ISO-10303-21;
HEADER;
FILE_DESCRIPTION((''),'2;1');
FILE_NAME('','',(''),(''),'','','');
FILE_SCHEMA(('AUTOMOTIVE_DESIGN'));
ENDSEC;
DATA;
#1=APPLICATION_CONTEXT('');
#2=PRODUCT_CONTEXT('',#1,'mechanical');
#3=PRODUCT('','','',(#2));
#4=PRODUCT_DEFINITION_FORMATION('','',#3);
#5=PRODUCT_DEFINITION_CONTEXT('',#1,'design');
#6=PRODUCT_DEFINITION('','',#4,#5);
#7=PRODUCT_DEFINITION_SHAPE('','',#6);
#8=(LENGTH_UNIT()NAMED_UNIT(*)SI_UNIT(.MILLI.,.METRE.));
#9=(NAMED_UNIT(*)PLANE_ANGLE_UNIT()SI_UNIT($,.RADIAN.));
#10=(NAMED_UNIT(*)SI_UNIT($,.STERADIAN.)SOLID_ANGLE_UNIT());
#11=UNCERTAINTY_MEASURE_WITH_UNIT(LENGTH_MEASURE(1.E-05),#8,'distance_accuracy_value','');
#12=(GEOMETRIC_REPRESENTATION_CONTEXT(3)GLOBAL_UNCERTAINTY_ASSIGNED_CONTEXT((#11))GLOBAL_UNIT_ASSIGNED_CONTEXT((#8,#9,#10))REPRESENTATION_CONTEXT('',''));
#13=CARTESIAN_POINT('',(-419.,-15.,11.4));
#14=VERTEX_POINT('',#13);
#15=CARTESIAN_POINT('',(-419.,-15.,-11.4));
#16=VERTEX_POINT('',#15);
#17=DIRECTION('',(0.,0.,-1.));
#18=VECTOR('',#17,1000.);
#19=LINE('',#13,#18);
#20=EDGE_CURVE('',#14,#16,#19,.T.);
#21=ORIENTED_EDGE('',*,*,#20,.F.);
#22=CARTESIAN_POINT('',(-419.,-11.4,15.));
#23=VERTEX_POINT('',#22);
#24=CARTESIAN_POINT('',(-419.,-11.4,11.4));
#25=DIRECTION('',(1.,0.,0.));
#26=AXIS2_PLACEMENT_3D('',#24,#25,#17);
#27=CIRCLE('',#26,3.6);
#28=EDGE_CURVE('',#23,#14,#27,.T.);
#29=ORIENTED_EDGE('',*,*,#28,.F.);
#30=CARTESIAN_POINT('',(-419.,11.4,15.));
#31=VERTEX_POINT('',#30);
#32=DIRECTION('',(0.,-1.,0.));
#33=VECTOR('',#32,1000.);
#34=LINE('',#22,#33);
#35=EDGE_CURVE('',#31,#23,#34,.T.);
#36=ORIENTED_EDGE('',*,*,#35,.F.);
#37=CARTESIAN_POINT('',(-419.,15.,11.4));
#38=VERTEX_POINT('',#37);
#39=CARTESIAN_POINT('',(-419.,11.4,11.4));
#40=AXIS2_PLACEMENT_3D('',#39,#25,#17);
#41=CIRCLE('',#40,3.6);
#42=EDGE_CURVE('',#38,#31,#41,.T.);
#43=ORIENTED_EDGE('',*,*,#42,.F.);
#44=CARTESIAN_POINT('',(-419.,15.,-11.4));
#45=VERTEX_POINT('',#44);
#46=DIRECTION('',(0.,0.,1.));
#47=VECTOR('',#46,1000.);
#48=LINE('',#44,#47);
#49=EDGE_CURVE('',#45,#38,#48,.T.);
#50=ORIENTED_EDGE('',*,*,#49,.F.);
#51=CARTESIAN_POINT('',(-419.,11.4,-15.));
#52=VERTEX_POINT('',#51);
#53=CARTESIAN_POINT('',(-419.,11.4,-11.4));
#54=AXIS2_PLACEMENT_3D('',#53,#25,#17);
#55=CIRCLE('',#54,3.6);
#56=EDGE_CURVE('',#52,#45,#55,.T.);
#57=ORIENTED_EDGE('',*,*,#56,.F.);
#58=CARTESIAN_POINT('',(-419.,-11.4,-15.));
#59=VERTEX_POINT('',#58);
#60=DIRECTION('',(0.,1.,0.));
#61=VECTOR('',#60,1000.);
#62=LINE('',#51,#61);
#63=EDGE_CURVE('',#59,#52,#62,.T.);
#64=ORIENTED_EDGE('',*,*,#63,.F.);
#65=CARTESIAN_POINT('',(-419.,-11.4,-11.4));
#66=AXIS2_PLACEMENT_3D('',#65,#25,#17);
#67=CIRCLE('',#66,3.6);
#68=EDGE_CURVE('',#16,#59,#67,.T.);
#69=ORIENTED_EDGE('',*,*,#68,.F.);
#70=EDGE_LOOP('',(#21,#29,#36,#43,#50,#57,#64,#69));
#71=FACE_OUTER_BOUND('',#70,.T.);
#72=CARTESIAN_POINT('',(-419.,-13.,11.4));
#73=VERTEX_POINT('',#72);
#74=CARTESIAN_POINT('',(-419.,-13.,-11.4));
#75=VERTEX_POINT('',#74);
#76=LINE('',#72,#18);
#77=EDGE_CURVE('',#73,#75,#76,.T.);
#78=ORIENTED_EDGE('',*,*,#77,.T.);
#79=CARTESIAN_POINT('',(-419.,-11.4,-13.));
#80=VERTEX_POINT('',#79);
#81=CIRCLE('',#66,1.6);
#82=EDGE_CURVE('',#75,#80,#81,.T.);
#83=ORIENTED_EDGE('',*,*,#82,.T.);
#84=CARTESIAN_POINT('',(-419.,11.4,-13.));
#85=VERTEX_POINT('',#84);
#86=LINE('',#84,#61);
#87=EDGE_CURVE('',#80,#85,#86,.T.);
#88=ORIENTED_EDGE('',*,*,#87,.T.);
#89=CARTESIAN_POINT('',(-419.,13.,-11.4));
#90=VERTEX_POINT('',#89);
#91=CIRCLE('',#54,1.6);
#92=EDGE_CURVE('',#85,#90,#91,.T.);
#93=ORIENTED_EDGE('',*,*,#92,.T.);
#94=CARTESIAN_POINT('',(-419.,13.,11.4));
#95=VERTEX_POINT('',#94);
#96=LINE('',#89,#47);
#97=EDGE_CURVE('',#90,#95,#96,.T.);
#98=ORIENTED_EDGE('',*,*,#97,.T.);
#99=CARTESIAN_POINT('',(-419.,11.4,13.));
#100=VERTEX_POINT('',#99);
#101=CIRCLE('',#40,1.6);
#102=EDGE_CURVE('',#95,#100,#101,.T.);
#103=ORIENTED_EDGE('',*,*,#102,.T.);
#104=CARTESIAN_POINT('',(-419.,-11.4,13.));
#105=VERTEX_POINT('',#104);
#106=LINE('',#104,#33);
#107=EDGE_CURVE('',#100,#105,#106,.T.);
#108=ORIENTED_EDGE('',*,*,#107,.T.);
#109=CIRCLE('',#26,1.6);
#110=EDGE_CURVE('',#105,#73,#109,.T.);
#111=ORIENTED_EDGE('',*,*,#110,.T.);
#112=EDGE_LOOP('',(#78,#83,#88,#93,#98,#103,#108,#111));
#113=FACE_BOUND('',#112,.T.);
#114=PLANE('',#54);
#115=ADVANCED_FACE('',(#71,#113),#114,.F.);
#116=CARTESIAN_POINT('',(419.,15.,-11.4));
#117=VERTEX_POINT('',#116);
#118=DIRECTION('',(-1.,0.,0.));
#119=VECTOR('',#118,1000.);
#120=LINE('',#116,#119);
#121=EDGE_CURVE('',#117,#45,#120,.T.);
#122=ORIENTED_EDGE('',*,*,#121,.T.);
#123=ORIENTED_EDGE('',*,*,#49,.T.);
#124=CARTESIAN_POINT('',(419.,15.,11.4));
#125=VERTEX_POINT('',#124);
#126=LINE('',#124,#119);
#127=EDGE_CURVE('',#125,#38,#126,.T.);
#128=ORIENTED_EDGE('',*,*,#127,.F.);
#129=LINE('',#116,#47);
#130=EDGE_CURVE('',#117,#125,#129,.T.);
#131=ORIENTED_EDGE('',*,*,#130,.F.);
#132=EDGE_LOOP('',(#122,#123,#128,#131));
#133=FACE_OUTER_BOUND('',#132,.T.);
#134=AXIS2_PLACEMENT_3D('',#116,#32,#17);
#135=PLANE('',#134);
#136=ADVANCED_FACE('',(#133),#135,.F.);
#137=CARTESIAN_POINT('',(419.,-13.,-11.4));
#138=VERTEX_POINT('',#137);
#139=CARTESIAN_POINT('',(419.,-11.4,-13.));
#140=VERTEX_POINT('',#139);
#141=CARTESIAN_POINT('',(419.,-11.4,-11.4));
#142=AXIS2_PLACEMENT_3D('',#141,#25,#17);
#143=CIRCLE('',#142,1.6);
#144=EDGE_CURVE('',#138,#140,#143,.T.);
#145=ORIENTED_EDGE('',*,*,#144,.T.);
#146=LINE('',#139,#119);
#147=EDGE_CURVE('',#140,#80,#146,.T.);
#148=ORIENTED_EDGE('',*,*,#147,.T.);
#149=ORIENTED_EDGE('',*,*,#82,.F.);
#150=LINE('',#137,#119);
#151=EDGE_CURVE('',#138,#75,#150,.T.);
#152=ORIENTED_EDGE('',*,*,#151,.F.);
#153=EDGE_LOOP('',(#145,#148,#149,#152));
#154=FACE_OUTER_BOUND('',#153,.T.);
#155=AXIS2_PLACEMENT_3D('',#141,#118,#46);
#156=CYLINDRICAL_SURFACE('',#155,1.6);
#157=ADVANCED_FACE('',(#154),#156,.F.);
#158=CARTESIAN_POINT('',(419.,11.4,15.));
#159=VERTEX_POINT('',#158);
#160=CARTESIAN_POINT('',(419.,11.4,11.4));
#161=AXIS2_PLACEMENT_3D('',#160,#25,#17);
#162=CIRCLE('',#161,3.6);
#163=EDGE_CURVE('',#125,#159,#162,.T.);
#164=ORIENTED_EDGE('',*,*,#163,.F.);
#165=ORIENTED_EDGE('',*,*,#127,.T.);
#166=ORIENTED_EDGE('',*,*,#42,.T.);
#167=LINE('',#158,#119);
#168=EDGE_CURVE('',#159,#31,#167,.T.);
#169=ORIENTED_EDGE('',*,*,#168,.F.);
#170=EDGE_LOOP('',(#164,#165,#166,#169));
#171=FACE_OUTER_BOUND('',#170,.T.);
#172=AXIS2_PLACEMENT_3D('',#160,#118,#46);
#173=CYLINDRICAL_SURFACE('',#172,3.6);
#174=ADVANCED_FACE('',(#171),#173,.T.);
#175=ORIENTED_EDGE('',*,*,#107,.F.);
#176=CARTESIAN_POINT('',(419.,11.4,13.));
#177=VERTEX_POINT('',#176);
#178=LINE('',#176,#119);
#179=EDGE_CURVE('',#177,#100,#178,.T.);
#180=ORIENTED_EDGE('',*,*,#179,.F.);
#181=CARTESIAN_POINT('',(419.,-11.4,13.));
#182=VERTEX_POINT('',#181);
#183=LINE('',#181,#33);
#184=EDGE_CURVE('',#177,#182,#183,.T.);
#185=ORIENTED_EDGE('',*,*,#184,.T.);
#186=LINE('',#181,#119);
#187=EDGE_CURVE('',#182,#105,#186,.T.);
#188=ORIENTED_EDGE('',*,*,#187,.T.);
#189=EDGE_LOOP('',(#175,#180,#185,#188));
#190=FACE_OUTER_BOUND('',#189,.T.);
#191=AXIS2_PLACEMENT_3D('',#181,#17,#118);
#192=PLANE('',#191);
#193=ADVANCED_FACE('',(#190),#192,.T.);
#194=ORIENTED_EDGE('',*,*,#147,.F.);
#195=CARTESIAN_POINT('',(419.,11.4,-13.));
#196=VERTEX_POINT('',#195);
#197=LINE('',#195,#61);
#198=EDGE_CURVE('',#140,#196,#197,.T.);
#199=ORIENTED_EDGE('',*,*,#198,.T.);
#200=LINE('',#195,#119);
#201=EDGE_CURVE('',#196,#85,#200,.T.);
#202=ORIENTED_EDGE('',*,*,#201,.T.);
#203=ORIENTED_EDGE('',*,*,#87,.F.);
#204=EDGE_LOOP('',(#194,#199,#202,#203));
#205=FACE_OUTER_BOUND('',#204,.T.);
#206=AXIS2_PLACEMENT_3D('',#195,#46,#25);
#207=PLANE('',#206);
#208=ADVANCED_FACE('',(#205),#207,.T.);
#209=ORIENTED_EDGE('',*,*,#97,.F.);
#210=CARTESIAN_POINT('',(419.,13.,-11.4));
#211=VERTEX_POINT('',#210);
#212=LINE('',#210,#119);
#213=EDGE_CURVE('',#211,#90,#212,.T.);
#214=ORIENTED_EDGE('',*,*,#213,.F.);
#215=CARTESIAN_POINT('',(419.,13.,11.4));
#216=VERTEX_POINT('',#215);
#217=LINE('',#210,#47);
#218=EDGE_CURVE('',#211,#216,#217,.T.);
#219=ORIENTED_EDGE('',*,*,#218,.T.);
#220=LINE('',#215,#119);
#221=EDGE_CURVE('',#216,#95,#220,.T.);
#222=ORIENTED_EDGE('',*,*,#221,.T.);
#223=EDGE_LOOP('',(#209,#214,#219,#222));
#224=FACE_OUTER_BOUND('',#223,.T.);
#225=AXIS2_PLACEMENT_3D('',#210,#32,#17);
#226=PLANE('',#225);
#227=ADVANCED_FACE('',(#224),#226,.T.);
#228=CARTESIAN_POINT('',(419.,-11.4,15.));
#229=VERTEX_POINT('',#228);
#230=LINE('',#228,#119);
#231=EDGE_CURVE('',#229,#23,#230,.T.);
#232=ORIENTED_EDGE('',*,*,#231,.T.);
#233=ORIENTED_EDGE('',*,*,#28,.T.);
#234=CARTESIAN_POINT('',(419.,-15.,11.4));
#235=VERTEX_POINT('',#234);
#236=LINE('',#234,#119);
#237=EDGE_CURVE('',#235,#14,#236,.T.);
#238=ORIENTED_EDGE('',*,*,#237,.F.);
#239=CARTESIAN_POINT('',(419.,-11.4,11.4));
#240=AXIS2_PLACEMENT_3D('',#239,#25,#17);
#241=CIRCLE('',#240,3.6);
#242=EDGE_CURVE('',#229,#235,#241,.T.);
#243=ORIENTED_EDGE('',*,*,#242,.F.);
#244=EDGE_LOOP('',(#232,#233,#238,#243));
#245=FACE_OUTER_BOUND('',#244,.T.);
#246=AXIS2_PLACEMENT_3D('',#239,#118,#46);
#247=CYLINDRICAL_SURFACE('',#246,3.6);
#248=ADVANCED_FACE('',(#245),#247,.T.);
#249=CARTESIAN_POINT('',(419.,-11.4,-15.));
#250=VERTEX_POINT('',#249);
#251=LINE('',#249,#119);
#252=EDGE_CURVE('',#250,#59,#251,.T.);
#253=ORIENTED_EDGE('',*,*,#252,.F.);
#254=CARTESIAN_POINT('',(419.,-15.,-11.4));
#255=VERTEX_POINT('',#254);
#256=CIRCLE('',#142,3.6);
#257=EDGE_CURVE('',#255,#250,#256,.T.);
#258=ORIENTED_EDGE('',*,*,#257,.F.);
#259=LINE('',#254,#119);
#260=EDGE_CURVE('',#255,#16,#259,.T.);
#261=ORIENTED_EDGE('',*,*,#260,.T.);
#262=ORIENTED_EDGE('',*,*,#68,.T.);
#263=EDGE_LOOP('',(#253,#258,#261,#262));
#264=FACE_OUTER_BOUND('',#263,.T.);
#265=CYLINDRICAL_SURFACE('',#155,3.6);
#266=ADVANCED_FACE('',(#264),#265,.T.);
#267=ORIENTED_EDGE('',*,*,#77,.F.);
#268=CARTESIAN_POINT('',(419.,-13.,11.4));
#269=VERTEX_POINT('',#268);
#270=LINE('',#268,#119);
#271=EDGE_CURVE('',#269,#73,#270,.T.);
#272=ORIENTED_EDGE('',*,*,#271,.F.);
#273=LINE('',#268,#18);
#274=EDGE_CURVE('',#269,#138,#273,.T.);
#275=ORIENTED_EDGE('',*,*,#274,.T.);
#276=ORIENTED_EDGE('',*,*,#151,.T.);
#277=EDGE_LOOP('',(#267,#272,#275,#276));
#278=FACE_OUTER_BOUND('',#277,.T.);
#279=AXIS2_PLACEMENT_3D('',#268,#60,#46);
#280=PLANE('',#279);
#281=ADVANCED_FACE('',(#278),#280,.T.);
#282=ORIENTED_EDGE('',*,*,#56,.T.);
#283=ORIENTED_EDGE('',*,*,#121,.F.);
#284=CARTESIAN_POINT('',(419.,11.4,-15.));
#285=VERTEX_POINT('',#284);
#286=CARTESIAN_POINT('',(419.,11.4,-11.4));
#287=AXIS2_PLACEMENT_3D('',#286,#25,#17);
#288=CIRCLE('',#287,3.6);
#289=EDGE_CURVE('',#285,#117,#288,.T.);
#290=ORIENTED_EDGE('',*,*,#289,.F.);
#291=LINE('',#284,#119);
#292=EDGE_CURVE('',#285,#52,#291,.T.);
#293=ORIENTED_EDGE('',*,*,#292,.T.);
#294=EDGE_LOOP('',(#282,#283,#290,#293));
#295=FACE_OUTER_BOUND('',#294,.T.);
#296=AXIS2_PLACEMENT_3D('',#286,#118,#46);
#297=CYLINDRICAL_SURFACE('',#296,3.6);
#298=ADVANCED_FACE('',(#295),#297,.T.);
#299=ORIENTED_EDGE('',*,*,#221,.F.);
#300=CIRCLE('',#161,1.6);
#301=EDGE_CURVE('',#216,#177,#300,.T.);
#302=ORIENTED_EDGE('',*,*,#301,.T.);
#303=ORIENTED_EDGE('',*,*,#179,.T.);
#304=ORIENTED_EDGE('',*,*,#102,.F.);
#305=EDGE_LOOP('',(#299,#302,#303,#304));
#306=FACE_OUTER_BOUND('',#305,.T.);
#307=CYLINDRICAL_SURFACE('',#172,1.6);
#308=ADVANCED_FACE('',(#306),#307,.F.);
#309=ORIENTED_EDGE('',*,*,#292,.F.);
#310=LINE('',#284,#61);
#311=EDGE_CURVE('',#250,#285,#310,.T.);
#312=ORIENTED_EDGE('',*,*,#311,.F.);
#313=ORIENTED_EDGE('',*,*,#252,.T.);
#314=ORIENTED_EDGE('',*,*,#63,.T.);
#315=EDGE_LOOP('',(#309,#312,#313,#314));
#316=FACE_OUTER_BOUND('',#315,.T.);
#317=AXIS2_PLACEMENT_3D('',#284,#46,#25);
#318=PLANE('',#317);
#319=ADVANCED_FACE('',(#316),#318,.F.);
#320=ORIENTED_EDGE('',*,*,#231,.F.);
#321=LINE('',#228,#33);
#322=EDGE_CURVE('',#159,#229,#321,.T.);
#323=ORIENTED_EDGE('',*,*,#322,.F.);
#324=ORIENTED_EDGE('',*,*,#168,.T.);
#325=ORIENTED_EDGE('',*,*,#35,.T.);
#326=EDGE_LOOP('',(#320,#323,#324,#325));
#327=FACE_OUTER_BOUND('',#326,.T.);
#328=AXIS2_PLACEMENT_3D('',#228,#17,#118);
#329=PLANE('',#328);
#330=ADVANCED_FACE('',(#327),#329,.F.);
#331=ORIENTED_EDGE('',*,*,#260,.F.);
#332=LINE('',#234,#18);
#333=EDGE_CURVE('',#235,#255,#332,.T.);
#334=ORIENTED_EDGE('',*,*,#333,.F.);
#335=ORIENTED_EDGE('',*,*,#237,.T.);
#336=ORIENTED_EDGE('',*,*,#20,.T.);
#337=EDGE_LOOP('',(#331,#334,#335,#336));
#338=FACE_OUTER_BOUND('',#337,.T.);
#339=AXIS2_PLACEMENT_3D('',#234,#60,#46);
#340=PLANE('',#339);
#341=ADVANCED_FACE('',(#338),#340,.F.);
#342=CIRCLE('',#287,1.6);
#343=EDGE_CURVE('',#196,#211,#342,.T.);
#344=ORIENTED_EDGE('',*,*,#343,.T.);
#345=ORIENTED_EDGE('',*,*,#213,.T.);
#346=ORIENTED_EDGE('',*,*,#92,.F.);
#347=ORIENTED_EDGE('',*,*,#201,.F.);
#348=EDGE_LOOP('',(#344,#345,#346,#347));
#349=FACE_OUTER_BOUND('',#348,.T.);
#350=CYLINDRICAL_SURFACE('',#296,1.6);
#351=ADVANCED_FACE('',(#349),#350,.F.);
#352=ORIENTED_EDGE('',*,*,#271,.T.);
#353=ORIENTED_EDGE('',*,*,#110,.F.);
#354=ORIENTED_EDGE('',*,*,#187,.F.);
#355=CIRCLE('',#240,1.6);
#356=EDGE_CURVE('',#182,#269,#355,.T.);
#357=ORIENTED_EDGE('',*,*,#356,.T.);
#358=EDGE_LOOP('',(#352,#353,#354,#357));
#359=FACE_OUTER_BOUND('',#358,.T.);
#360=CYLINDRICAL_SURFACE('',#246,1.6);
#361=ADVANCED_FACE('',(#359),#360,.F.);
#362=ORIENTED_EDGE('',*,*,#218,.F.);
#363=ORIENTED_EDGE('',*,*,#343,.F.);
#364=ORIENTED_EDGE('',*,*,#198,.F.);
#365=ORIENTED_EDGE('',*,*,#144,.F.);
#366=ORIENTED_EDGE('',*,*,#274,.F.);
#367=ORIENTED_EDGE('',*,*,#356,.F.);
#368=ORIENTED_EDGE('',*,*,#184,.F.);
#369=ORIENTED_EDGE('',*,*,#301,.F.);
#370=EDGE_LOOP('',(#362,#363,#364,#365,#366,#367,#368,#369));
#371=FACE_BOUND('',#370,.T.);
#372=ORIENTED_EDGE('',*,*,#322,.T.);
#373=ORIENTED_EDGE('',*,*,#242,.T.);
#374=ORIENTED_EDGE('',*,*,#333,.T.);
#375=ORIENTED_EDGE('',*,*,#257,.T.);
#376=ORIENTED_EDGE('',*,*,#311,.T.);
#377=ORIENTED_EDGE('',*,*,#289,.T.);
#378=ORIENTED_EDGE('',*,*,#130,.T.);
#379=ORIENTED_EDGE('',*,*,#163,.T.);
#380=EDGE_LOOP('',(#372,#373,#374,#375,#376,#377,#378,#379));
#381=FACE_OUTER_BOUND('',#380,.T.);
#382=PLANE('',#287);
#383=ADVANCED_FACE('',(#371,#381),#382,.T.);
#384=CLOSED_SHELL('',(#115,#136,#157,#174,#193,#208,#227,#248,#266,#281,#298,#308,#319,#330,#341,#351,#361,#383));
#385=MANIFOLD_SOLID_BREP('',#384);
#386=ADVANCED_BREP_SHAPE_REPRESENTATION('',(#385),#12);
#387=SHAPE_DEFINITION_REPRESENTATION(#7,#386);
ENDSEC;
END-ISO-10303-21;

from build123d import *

# Parameters (mm, degrees)
MEMBER_30_2_1_DEPTH = 838


with BuildPart() as part:
    # Sketch1 → Member 30_2_1 (new body)
    with BuildSketch(Plane(origin=(-419, 0, 0), x_dir=(0, 0, -1), z_dir=(1, 0, 0))):
        with BuildLine():
            Line((-11.4, -15), (11.4, -15))
            ThreePointArc((11.4, -15), (13.945584412, -13.945584412), (15, -11.4))
            Line((15, -11.4), (15, 11.4))
            ThreePointArc((15, 11.4), (13.945584412, 13.945584412), (11.4, 15))
            Line((11.4, 15), (-11.4, 15))
            ThreePointArc((-11.4, 15), (-13.945584412, 13.945584412), (-15, 11.4))
            Line((-15, 11.4), (-15, -11.4))
            ThreePointArc((-15, -11.4), (-13.945584412, -13.945584412), (-11.4, -15))
        make_face()
        with BuildLine():
            Line((-11.4, -13), (11.4, -13))
            ThreePointArc((11.4, -13), (12.53137085, -12.53137085), (13, -11.4))
            Line((13, -11.4), (13, 11.4))
            ThreePointArc((13, 11.4), (12.53137085, 12.53137085), (11.4, 13))
            Line((11.4, 13), (-11.4, 13))
            ThreePointArc((-11.4, 13), (-12.53137085, 12.53137085), (-13, 11.4))
            Line((-13, 11.4), (-13, -11.4))
            ThreePointArc((-13, -11.4), (-12.53137085, -12.53137085), (-11.4, -13))
        make_face(mode=Mode.SUBTRACT)
    extrude(amount=MEMBER_30_2_1_DEPTH)


solid = part.part
